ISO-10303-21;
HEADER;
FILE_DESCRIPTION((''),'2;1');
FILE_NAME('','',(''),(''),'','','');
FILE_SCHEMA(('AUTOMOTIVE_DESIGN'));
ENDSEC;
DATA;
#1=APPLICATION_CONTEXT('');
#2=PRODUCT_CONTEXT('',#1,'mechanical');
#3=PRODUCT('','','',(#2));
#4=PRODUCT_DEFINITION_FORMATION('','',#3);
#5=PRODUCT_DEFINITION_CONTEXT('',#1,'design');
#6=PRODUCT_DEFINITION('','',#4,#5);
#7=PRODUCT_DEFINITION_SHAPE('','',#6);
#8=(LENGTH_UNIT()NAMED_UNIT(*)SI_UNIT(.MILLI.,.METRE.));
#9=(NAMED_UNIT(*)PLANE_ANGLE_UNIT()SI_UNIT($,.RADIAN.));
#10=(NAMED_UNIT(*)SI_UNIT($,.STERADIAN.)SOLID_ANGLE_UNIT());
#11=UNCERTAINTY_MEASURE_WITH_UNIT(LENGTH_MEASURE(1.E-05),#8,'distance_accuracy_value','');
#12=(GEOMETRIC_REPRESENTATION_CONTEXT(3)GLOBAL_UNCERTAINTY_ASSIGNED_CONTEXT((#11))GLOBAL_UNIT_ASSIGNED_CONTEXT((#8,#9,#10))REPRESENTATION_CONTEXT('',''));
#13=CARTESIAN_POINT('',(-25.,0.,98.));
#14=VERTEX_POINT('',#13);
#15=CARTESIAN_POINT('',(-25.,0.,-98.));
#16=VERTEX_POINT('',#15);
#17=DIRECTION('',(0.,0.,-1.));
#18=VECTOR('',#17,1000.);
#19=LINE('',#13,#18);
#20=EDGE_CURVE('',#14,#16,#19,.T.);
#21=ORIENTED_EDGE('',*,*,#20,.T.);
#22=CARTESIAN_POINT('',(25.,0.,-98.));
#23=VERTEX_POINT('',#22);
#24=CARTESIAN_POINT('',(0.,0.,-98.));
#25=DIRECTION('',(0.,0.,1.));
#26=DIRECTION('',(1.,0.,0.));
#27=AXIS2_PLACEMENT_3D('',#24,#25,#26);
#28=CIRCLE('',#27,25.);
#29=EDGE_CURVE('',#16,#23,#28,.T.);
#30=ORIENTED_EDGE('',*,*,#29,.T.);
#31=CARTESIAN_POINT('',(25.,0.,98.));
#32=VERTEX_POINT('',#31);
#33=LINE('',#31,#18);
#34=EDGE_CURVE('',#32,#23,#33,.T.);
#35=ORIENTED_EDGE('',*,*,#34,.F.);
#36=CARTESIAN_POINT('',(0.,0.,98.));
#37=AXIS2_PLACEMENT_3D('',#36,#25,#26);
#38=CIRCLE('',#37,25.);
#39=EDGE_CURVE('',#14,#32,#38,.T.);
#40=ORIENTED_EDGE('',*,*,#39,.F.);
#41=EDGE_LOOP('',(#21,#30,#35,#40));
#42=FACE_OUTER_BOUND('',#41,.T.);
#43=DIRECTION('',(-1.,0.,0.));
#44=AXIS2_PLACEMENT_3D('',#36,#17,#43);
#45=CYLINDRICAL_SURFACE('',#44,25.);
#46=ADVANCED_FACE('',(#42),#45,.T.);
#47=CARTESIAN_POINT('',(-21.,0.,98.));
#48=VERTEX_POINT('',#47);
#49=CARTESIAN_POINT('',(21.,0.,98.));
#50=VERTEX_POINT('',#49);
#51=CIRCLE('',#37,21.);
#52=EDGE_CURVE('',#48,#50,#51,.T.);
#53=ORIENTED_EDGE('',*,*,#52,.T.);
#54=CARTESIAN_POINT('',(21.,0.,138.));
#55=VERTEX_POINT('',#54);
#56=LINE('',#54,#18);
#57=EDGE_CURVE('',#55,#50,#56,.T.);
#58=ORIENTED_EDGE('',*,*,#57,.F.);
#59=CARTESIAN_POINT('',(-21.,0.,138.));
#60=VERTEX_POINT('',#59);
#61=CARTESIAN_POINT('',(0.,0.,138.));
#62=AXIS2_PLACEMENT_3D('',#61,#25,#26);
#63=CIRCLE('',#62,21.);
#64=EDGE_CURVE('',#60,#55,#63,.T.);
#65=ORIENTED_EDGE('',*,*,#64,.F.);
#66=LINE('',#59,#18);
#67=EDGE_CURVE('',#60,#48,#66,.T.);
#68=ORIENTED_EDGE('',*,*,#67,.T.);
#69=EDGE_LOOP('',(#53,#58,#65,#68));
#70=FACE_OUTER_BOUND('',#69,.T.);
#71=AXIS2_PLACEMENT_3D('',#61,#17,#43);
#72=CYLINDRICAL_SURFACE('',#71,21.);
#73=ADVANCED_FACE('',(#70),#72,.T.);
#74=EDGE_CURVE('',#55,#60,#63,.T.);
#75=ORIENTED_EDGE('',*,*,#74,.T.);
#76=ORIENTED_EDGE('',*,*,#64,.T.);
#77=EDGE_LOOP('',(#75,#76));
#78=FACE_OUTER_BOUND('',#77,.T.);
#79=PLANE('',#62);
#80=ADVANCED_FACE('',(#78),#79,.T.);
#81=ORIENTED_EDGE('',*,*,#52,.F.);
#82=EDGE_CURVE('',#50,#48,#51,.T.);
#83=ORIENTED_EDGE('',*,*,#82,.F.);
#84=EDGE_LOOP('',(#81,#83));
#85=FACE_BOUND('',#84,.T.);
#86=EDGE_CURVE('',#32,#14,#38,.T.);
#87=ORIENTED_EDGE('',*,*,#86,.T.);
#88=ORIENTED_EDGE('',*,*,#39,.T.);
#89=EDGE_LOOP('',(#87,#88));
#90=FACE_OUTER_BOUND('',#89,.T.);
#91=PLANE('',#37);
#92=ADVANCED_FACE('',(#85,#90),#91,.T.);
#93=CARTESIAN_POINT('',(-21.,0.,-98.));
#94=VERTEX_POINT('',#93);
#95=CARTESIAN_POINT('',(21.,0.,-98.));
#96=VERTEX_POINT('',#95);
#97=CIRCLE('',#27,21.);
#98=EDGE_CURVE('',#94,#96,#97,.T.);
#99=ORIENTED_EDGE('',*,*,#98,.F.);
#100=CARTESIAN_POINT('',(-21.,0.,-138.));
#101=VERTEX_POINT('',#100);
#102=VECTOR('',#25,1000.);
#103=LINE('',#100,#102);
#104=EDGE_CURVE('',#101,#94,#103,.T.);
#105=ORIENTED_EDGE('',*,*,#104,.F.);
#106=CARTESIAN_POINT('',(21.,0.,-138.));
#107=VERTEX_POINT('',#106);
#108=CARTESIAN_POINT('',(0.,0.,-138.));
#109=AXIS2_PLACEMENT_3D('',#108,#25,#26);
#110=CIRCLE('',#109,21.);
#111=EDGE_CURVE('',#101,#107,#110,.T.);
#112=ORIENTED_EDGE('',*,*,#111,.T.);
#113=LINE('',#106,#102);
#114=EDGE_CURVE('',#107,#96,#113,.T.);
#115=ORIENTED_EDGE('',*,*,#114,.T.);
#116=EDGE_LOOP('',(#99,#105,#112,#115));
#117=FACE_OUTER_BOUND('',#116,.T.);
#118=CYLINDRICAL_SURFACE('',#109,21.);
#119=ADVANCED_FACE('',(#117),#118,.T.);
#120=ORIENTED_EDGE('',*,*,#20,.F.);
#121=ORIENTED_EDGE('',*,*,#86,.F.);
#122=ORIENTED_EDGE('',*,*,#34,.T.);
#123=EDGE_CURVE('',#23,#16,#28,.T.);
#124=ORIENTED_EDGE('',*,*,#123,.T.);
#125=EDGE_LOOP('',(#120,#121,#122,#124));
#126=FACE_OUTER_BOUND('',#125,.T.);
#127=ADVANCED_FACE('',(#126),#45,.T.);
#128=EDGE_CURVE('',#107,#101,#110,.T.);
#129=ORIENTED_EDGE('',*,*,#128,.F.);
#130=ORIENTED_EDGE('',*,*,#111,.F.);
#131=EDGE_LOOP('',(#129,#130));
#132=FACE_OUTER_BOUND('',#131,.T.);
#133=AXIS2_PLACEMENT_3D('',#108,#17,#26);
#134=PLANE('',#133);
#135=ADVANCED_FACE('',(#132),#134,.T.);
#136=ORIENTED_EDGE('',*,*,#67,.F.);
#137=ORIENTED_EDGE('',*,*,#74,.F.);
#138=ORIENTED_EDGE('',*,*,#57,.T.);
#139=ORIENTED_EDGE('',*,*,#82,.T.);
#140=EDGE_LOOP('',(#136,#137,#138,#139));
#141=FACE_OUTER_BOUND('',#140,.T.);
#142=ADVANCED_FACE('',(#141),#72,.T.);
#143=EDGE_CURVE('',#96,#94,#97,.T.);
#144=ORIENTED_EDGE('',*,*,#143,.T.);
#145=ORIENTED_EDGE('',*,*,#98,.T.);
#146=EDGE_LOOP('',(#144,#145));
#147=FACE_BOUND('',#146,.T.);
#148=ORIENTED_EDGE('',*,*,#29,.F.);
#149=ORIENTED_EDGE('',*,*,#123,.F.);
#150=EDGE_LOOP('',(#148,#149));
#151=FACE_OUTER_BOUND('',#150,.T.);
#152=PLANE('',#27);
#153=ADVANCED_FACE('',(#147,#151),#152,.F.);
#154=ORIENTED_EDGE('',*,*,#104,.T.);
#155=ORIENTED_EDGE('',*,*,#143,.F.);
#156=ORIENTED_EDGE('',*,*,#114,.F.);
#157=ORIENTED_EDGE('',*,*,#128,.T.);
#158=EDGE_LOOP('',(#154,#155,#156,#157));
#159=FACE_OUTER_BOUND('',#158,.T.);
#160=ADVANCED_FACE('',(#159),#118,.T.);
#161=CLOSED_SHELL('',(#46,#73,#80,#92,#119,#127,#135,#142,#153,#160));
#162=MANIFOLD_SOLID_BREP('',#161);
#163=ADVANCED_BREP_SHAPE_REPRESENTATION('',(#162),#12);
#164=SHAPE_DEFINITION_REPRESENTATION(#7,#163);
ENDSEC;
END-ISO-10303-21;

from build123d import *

# Parameters (mm, degrees)
SKETCH_1_R           = 25
BOSS_EXTRUDE_1_DEPTH = 98
SKETCH_2_R           = 21
BOSS_EXTRUDE_2_DEPTH = 40


with BuildPart() as part:
    # Sketch 1 → Boss-Extrude 1 (new, symmetric)
    with BuildSketch(Plane.XY):
        Circle(SKETCH_1_R)
    extrude(amount=BOSS_EXTRUDE_1_DEPTH, both=True)

    # Sketch 2 → Boss-Extrude 2 (add)
    with BuildSketch(Plane.XY.offset(98)):
        Circle(SKETCH_2_R)
    boss_extrude_2 = extrude(amount=BOSS_EXTRUDE_2_DEPTH)

    # Mirror 1: Boss-Extrude 2 across plane
    add(boss_extrude_2.mirror(Plane.XY))


solid = part.part
